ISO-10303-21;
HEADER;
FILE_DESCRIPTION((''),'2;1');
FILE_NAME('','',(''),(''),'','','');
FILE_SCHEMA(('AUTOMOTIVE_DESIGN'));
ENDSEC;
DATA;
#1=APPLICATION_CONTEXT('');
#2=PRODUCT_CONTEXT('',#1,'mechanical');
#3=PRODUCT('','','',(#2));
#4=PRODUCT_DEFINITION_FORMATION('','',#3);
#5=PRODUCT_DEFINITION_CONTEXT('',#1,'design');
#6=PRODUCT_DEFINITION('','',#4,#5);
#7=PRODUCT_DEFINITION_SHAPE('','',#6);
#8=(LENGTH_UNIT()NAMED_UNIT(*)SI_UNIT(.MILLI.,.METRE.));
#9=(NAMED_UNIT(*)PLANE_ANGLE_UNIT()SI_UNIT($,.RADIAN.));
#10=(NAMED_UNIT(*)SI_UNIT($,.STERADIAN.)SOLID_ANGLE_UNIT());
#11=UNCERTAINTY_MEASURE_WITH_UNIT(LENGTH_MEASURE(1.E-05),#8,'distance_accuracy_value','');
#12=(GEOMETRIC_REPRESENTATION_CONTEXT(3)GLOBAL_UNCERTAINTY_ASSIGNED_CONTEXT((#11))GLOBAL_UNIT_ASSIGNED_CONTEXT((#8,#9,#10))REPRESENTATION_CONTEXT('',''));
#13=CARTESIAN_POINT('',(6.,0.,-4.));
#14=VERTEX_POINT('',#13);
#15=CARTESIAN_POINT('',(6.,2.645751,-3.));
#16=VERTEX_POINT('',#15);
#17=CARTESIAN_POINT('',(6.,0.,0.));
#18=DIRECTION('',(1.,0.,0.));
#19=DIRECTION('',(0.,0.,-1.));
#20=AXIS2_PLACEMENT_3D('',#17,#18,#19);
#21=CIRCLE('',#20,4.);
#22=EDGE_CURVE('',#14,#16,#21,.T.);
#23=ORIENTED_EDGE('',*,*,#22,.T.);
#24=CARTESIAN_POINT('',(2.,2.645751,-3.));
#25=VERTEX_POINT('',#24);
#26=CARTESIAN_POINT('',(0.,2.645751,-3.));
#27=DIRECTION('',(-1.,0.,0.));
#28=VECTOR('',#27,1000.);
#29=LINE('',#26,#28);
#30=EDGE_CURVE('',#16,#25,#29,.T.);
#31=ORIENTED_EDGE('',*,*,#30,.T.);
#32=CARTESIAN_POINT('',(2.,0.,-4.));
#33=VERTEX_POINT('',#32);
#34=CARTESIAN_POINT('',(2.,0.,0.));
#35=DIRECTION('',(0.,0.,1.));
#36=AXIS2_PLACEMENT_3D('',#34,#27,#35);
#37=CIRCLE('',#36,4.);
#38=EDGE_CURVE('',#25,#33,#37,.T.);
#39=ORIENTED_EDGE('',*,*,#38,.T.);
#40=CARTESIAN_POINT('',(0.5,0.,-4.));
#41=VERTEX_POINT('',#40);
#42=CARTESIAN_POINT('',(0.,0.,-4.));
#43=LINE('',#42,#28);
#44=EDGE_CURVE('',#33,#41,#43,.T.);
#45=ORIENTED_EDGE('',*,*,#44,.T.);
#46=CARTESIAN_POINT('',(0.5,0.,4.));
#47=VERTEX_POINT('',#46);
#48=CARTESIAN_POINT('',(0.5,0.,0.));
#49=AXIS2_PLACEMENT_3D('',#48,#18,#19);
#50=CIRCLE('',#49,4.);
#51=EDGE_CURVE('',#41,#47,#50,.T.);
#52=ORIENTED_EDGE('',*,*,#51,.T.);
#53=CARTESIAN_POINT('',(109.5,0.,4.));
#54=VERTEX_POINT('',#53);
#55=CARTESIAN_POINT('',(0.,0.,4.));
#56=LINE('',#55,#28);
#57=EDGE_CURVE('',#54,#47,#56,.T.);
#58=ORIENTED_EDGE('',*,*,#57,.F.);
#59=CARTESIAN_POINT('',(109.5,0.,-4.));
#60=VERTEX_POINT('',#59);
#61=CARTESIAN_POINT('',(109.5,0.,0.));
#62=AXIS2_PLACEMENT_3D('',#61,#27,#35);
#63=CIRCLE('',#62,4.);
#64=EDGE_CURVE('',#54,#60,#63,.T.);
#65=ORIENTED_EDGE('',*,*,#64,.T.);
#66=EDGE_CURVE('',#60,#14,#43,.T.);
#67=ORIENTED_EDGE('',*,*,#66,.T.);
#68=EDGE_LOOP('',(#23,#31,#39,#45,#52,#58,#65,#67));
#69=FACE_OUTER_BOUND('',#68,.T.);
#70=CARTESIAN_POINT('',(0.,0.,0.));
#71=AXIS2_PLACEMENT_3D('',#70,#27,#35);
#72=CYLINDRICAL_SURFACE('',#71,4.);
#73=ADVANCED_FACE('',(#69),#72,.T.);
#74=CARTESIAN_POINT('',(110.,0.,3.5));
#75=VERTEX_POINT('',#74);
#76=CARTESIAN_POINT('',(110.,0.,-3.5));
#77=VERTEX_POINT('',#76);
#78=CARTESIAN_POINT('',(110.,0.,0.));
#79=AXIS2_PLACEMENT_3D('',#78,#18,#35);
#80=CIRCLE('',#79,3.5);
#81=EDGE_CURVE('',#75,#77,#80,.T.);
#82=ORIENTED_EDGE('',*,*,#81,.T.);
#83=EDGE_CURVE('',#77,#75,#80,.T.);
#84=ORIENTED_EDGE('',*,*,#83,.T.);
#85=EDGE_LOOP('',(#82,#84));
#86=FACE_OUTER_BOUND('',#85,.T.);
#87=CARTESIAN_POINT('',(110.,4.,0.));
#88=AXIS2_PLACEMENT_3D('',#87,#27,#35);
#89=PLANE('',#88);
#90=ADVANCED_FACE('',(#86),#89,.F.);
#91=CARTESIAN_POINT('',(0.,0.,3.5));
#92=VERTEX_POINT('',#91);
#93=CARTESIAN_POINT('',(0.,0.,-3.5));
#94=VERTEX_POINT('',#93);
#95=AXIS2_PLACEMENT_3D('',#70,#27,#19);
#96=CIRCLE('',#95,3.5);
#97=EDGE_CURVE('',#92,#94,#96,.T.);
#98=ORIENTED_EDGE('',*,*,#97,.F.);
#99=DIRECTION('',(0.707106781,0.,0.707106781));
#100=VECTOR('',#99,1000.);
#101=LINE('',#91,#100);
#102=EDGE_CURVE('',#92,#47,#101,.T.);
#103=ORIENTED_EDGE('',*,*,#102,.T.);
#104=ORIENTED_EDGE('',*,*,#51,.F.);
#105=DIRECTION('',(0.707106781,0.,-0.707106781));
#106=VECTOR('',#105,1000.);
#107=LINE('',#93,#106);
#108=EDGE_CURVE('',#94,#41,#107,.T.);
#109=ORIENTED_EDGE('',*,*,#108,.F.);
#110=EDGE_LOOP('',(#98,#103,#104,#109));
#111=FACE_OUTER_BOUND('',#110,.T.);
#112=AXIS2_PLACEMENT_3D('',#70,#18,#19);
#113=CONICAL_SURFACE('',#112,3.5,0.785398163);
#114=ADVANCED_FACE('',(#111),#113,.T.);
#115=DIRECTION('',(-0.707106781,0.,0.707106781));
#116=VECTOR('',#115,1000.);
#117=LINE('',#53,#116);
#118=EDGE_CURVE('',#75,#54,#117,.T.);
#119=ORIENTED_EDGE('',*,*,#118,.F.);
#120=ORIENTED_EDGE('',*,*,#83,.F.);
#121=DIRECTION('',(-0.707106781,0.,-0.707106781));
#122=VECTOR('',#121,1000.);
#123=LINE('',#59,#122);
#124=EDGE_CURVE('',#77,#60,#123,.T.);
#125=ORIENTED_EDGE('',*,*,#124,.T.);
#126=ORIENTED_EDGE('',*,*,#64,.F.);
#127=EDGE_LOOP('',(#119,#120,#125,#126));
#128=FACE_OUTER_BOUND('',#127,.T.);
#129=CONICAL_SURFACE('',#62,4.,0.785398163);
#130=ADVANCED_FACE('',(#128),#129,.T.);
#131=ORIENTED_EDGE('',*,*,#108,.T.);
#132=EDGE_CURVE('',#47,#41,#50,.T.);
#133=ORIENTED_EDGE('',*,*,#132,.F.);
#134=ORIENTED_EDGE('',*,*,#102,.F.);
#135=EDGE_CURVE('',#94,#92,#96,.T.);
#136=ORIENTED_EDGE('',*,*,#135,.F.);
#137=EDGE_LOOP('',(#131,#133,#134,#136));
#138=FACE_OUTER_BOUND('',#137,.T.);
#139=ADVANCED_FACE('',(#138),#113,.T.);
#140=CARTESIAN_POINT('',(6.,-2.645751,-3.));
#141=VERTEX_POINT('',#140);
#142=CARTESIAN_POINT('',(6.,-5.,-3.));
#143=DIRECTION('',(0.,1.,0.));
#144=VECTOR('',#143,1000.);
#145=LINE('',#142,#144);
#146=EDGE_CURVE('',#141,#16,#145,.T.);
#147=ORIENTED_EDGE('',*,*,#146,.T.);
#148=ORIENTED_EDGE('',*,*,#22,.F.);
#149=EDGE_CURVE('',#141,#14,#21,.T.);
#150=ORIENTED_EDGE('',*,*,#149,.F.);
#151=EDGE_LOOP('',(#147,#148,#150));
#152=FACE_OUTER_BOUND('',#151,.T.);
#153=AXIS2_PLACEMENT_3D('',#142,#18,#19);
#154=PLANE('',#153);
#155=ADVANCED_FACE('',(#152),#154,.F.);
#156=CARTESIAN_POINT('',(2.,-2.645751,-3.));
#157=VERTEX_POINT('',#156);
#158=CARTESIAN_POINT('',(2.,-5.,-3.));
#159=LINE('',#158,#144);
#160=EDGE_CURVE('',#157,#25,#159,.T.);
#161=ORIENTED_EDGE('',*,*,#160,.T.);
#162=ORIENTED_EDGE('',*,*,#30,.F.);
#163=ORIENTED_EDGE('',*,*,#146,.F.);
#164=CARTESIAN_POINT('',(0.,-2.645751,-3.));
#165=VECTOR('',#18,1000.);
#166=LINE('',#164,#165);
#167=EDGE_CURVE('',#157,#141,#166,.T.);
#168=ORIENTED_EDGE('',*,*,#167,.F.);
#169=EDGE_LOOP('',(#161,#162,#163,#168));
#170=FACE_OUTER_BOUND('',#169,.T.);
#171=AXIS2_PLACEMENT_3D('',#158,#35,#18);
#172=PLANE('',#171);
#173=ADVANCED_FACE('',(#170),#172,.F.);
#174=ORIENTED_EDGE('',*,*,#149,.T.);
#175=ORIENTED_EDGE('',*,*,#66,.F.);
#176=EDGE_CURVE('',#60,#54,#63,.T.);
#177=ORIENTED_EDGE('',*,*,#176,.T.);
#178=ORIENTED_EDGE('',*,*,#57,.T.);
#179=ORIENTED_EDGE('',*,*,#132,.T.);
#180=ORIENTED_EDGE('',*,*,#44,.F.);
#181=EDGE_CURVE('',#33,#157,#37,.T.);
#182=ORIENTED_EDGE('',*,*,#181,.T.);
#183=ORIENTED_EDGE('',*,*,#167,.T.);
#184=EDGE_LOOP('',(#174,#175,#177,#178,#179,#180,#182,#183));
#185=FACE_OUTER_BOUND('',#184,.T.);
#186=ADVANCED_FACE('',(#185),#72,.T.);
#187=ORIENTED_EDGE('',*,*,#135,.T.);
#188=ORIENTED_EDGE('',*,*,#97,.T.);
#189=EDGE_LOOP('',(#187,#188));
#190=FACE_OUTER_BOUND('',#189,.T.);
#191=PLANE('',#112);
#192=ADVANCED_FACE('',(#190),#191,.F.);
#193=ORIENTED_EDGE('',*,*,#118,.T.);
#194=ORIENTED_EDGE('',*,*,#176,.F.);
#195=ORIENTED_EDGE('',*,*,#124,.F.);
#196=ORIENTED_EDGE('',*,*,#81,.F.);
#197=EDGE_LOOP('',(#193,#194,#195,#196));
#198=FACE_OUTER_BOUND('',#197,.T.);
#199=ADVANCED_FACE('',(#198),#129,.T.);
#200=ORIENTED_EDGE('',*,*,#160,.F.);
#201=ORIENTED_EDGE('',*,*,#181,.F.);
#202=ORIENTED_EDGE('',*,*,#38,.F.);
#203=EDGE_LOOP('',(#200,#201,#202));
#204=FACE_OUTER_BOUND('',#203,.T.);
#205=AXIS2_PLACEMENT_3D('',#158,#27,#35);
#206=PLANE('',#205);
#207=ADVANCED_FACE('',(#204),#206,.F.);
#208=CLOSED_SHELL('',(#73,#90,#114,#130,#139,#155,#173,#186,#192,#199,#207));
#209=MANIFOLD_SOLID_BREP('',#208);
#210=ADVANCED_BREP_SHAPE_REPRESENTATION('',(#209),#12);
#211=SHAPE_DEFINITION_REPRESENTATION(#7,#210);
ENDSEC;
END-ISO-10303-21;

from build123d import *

# Parameters (mm, degrees)
SKETCH1_W          = 110
SKETCH1_H          = 4
SKETCH2_W          = 4
SKETCH2_H          = 2
CUT_EXTRUDE1_DEPTH = 5
CHAMFER1_SIZE      = 0.5


with BuildPart() as part:
    # Sketch1 → Revolve1 (revolve)
    with BuildSketch(Plane.XY, mode=Mode.PRIVATE) as revolve1_sk:
        with Locations((55, 2)):
            Rectangle(SKETCH1_W, SKETCH1_H)
    revolve(revolve1_sk.sketch.rotate(Axis((0, 0, 0), (1, 0, 0)), 90), axis=Axis((0, 0, 0), (1, 0, 0)))

    # Sketch2 → Cut-Extrude1 (cut, symmetric)
    with BuildSketch(Plane(origin=(0, 0, 0), x_dir=(1, 0, 0), z_dir=(0, 1, 0))):
        with Locations((4, 4)):
            Rectangle(SKETCH2_W, SKETCH2_H)
    extrude(amount=CUT_EXTRUDE1_DEPTH, both=True, mode=Mode.SUBTRACT)

    # Chamfer1
    chamfer1_edges = [part.edges().sort_by_distance(p)[0] for p in [
        (110, 0, -4),
        (0, 0, -4),
    ]]
    chamfer(chamfer1_edges, length=CHAMFER1_SIZE)


solid = part.part
